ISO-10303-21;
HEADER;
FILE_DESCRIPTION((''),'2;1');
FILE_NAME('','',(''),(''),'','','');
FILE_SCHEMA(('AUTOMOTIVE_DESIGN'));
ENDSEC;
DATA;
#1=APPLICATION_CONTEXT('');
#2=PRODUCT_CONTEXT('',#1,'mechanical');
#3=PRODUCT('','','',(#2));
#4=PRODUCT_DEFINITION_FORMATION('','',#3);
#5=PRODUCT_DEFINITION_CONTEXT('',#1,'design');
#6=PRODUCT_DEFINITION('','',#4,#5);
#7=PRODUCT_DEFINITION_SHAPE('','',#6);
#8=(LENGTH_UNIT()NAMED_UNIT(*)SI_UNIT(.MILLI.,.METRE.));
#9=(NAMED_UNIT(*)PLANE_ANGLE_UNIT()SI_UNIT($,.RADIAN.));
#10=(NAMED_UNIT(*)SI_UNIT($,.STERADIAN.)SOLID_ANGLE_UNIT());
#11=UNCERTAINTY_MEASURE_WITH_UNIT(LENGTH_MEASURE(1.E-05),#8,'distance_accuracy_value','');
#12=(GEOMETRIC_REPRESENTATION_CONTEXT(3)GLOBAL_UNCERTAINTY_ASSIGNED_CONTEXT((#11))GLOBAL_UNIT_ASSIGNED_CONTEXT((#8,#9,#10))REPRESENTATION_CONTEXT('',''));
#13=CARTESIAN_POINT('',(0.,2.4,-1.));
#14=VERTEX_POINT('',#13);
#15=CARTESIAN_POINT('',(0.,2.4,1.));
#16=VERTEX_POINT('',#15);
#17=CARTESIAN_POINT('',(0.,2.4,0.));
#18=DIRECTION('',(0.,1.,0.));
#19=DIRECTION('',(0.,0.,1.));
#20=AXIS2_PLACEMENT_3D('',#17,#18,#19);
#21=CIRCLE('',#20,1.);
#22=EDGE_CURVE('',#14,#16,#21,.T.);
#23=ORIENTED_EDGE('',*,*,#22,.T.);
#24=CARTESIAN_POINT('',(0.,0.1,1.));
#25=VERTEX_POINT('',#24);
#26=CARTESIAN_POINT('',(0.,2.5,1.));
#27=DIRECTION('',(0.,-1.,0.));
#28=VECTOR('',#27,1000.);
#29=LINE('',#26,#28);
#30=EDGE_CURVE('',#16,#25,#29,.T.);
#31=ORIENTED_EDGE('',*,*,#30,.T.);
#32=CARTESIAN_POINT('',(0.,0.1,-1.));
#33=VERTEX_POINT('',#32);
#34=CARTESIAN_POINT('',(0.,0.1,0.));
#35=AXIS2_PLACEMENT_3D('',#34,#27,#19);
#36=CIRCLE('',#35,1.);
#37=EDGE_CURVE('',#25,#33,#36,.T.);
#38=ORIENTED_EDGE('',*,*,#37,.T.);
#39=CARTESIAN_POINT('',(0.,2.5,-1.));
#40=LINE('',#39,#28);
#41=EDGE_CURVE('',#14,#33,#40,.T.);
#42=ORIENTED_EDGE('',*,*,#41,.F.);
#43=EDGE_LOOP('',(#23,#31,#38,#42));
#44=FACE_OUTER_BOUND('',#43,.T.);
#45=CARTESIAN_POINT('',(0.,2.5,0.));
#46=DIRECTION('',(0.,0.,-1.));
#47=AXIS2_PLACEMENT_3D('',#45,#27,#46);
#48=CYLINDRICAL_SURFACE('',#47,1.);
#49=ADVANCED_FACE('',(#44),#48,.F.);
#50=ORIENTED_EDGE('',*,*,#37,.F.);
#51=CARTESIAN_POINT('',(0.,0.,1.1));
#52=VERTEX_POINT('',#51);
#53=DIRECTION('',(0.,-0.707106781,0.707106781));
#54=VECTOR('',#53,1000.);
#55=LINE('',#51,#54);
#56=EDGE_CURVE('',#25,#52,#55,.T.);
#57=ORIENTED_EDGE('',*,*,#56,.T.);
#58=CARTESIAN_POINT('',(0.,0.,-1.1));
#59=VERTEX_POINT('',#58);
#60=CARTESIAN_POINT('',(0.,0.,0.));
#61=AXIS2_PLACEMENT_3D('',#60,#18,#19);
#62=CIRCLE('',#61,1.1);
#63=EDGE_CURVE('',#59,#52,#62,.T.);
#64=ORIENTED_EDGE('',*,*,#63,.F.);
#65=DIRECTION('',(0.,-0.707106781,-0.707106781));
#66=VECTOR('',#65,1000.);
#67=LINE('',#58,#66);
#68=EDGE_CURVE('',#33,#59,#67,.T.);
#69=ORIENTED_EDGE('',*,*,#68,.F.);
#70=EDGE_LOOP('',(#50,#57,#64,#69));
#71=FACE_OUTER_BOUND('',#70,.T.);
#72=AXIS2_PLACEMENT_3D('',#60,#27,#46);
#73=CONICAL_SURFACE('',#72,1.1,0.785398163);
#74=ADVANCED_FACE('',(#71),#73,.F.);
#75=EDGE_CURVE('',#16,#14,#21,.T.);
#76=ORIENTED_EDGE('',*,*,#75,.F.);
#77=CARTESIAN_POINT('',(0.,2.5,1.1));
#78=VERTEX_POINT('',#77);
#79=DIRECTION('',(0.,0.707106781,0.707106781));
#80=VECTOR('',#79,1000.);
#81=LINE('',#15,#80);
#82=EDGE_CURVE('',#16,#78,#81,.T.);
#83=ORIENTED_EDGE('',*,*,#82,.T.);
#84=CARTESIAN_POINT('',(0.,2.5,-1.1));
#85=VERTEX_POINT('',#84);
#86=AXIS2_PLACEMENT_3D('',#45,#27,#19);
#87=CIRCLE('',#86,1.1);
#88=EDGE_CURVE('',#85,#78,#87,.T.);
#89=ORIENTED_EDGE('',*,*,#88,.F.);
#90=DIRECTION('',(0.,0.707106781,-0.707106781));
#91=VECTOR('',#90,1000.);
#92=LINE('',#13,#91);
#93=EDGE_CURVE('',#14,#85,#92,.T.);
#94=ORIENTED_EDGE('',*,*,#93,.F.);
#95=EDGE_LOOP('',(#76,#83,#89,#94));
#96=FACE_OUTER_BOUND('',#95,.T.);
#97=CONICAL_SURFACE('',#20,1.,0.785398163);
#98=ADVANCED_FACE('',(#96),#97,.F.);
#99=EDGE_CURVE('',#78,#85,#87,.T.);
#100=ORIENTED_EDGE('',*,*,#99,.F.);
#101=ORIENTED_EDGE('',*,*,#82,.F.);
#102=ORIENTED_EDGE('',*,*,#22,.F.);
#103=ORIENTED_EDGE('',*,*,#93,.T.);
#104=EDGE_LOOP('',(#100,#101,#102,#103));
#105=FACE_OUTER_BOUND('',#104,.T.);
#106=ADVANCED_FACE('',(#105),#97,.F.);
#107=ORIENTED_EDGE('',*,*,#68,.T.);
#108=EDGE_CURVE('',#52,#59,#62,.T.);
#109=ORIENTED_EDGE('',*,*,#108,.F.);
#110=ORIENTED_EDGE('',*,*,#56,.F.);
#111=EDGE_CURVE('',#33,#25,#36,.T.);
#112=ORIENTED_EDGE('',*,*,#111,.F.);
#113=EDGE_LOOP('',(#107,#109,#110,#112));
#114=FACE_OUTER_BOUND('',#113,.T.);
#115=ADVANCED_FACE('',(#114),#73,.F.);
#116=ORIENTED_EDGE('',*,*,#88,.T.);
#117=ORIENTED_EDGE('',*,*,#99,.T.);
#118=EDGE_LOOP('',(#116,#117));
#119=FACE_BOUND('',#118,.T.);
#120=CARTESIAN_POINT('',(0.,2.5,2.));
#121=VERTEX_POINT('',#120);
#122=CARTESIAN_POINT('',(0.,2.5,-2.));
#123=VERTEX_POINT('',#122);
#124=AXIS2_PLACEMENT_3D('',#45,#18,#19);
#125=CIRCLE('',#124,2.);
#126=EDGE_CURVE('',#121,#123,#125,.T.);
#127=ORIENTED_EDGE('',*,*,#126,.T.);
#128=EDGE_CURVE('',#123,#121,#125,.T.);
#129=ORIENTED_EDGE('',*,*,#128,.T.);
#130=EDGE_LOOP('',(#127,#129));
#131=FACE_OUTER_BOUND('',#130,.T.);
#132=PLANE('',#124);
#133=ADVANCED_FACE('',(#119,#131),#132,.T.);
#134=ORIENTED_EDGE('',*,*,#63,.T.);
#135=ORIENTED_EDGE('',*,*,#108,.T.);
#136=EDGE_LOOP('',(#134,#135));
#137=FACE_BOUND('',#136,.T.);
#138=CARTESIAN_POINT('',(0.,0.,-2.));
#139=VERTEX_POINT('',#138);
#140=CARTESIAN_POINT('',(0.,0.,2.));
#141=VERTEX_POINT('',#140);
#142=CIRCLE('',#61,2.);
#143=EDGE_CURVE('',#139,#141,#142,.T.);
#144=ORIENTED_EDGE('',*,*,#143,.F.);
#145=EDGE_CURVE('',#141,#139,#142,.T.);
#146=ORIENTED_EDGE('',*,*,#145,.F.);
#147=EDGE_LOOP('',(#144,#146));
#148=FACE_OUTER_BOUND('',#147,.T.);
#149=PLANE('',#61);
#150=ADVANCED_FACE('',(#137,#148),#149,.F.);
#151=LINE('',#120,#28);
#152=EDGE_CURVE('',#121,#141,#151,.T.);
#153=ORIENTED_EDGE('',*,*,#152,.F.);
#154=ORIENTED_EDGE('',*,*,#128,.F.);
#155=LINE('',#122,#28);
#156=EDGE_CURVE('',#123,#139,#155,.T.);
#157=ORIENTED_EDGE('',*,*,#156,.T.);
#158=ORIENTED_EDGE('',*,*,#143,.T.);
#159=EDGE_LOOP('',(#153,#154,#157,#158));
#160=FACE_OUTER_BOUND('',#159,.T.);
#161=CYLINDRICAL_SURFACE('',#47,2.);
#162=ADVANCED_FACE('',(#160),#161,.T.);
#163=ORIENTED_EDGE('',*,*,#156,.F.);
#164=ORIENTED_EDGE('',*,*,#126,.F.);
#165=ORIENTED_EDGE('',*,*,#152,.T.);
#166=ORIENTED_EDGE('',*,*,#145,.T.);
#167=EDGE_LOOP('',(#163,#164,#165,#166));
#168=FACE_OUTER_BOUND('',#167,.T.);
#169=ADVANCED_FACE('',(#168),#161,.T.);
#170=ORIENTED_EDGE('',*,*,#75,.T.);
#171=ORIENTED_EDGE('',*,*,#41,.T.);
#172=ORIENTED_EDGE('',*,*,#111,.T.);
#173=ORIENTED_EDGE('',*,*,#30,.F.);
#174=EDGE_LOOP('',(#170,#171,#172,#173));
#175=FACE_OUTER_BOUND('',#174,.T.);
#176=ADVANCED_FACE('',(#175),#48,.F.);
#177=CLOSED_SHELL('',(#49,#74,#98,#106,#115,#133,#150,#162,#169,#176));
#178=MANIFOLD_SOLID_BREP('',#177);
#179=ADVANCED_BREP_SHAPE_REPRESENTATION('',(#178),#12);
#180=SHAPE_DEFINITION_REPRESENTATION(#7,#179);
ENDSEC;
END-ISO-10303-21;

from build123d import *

# Parameters (mm, degrees)
SKETCH_1_R          = 2
SKETCH_1_R_2        = 1
EXTRUDE_1_DEPTH     = 2.5
CHAMFER_C0_1_1_SIZE = 0.1


with BuildPart() as part:
    # 草图1 → 凸台-拉伸1 (new body)
    with BuildSketch(Plane(origin=(0, 0, 0), x_dir=(1, 0, 0), z_dir=(0, 1, 0))):
        with Locations(Location((0, 0, 0), (0, 0, 270))):
            Circle(SKETCH_1_R)
        with Locations(Location((0, 0, 0), (0, 0, 270))):
            Circle(SKETCH_1_R_2, mode=Mode.SUBTRACT)
    extrude(amount=EXTRUDE_1_DEPTH)

    # C0.1 倒角1
    chamfer_c0_1_1_edges = [part.edges().sort_by_distance(p)[0] for p in [
        (0, 0, -1),
        (0, 2.5, -1),
    ]]
    chamfer(chamfer_c0_1_1_edges, length=CHAMFER_C0_1_1_SIZE)


solid = part.part
